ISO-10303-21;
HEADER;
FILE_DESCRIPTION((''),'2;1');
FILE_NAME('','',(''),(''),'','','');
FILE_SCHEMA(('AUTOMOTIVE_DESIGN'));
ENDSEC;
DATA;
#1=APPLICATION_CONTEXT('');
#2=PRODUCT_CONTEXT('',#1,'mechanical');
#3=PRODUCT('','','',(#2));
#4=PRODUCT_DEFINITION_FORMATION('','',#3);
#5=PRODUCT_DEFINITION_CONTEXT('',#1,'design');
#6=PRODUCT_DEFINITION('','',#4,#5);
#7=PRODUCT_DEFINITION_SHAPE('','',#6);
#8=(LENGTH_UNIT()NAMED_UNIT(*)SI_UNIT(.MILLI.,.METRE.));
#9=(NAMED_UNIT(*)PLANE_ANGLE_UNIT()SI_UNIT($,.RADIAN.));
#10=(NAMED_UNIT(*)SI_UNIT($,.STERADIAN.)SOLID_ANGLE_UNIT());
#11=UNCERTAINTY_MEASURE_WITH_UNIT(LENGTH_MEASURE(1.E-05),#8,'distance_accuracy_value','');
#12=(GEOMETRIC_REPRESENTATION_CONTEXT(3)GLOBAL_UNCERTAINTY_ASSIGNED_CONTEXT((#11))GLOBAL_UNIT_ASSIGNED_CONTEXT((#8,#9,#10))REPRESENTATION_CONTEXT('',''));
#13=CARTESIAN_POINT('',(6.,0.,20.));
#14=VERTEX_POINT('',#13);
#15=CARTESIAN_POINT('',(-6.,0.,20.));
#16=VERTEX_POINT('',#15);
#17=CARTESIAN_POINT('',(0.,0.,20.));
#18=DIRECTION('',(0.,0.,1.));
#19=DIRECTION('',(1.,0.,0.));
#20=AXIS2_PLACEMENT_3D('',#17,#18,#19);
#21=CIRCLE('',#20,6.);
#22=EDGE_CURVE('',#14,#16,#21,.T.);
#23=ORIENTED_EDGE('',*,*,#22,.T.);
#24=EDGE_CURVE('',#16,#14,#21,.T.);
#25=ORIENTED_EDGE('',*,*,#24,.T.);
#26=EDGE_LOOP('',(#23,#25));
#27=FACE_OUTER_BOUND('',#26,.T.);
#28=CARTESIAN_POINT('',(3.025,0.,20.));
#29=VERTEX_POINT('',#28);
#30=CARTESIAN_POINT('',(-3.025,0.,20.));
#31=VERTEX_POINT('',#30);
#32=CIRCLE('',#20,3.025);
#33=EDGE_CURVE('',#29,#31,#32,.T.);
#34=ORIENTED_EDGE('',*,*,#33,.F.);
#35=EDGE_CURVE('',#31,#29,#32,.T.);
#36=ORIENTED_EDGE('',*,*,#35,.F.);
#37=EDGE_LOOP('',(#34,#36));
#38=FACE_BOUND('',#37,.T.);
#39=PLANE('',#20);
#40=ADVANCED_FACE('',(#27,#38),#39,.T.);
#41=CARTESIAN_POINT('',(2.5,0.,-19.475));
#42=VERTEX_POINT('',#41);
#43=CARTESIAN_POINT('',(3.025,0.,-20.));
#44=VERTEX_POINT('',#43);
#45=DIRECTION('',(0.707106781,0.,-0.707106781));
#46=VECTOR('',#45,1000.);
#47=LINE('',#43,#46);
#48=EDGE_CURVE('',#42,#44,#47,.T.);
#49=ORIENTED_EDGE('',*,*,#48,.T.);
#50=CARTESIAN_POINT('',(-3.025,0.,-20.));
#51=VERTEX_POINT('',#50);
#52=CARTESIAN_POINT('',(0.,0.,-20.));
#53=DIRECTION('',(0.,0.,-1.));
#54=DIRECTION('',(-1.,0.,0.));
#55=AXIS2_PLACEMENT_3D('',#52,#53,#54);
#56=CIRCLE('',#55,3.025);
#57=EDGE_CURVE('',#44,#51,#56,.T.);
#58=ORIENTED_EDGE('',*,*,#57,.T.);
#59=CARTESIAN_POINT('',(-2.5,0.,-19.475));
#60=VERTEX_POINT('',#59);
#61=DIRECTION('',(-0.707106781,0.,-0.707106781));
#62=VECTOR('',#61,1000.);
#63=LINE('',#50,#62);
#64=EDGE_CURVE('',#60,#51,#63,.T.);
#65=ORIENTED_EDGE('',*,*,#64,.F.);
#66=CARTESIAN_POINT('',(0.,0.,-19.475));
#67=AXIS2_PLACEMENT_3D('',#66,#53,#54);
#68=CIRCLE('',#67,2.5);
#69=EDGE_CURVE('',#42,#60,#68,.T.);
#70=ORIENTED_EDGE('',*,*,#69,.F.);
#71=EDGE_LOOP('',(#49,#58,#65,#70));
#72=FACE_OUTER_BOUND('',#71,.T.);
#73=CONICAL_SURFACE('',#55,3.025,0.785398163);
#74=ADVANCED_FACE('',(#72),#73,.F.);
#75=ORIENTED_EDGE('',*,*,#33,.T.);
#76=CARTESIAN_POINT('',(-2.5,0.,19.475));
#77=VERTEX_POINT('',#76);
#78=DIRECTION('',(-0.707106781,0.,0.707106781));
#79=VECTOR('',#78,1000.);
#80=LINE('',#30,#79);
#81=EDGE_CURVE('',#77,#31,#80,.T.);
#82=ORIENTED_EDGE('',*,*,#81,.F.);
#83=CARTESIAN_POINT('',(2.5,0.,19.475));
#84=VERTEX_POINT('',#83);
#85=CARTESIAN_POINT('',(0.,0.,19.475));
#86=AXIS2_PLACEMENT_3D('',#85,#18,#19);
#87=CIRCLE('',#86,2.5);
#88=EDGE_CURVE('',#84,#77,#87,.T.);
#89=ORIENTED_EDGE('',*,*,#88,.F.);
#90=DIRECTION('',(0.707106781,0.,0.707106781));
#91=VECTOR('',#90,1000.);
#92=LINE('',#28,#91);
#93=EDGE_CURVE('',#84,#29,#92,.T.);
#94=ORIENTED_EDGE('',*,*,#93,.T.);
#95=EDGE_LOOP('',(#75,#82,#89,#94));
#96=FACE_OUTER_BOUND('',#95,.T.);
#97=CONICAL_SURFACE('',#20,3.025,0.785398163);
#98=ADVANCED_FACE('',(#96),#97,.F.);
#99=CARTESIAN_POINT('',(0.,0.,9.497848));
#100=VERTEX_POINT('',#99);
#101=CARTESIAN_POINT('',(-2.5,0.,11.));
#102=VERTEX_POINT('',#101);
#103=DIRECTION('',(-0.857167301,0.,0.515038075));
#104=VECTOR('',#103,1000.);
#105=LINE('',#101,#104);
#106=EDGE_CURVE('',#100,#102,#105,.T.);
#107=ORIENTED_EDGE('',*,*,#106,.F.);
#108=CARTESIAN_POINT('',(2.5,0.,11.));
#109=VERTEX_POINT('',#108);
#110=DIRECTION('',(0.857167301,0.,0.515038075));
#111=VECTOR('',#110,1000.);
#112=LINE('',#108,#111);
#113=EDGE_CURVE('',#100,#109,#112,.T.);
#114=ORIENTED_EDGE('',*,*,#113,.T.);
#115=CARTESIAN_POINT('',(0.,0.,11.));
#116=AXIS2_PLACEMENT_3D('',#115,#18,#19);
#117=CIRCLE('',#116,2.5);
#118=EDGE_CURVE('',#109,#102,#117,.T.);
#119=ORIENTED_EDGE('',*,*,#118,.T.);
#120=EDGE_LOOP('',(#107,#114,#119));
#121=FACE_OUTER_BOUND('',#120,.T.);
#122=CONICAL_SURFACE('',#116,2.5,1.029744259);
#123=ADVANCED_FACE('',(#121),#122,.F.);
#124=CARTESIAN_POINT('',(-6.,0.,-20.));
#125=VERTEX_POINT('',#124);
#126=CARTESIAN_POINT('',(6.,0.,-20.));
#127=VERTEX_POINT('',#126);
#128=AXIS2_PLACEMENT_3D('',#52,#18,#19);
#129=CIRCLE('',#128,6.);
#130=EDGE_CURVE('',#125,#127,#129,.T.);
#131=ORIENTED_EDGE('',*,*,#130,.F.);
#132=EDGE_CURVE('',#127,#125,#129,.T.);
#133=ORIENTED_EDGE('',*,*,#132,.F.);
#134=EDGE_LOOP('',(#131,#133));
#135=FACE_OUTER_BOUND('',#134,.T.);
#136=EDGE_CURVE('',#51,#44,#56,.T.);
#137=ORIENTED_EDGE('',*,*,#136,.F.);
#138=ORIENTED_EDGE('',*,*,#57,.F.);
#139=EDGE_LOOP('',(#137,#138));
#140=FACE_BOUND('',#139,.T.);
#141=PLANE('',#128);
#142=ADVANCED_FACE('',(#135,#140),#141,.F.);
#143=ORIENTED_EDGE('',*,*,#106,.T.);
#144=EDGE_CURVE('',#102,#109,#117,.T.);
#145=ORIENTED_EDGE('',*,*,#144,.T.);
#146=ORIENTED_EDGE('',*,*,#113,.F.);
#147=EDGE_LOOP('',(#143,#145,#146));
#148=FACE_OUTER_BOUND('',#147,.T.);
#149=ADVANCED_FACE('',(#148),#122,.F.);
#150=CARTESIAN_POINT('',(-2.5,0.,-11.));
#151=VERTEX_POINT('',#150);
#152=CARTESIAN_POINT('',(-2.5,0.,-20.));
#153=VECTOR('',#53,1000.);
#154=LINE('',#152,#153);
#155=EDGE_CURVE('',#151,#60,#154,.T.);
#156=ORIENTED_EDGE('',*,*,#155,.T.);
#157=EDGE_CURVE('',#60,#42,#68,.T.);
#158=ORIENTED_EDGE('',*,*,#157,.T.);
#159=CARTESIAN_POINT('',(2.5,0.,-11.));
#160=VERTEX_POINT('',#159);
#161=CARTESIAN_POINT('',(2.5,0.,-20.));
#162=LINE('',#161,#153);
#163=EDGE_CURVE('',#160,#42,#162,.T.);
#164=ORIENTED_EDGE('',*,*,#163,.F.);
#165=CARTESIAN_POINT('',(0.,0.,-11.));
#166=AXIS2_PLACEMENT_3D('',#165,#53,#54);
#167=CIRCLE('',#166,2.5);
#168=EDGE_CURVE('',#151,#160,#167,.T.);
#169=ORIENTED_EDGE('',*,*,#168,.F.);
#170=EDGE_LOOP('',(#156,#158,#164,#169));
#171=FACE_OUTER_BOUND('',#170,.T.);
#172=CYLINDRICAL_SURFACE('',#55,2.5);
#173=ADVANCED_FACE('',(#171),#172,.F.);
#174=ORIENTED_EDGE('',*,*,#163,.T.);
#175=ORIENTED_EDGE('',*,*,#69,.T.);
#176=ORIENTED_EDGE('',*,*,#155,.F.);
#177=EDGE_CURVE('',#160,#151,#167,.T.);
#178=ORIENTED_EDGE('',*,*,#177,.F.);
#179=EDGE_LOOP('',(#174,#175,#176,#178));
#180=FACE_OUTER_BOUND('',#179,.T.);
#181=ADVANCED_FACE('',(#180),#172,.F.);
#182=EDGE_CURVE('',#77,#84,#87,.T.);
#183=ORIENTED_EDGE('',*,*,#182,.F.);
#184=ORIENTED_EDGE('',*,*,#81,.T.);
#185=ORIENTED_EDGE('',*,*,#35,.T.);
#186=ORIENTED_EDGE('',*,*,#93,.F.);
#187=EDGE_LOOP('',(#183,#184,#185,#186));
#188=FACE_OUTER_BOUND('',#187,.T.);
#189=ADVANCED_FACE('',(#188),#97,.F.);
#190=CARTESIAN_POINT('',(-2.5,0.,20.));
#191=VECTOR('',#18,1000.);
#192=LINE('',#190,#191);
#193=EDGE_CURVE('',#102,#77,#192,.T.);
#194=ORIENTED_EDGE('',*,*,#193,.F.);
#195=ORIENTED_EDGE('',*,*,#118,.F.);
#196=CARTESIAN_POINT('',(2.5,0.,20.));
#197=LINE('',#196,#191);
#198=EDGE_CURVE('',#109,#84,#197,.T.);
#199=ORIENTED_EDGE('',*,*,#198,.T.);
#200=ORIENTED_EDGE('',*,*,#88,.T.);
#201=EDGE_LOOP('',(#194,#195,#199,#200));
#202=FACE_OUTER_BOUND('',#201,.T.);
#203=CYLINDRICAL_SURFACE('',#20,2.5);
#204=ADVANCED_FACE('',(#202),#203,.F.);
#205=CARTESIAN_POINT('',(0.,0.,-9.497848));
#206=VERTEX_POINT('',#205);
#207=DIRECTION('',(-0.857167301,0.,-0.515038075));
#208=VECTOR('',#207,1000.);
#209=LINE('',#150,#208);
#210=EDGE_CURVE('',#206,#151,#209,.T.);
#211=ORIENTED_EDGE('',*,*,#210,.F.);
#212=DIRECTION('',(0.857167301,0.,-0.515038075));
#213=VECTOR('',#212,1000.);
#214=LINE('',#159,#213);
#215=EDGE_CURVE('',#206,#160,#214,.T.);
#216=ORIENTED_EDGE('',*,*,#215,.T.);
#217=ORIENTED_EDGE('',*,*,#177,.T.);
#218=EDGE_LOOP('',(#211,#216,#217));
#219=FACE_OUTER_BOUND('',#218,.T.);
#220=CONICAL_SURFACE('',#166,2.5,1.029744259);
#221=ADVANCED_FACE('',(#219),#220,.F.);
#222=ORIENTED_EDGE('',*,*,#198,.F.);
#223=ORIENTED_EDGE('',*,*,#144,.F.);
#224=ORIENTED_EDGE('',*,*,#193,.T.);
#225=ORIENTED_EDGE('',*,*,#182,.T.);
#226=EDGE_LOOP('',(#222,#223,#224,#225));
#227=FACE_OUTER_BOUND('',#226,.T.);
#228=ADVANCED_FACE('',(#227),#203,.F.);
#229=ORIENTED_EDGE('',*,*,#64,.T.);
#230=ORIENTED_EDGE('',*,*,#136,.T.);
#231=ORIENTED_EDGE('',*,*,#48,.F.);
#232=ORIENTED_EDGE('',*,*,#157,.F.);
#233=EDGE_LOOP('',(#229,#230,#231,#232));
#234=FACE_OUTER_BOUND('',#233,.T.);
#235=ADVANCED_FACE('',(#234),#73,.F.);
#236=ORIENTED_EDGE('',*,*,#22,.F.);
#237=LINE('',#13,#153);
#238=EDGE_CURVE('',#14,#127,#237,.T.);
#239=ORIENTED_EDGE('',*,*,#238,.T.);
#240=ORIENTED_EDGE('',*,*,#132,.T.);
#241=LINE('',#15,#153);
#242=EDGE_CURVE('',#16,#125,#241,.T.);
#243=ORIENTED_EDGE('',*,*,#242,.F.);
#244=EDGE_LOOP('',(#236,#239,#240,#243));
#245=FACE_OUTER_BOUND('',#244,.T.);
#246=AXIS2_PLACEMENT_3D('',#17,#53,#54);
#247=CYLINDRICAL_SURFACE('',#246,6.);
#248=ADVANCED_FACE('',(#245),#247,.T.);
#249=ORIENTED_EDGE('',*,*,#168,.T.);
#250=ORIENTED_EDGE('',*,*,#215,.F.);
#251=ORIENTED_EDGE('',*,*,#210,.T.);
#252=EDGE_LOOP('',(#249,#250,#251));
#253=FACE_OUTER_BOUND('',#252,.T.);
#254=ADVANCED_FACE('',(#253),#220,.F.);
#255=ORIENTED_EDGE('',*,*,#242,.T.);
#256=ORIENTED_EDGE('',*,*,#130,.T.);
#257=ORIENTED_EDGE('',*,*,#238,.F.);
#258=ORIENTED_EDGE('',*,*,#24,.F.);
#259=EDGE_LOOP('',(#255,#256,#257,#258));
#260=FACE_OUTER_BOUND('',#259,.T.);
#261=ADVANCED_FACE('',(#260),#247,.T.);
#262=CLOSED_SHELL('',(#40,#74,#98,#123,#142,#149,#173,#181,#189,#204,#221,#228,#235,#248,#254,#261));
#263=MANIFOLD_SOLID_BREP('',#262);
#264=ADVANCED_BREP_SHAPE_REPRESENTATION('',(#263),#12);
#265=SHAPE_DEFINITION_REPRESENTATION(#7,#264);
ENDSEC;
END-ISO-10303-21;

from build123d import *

# Parameters (mm, degrees)
SKETCH_1_R      = 6
EXTRUDE_1_DEPTH = 20


with BuildPart() as part:
    # 草图1 → 凸台-拉伸1 (new, symmetric)
    with BuildSketch(Plane.XY):
        Circle(SKETCH_1_R)
    extrude(amount=EXTRUDE_1_DEPTH, both=True)

    # 草图3 → M6 螺纹孔1 (revolve, cut)
    with BuildSketch(Plane(origin=(0, 0, 20), x_dir=(0, -1, 0), z_dir=(1, 0, 0))):
        Polygon((0, 0), (0, 10.502151548), (2.5, 9), (2.5, 0.525), (3.025, 0), align=None)
    hole_wizard_m6_1 = revolve(axis=Axis((0, 0, 26.35), (0, 0, -1)), mode=Mode.SUBTRACT)

    # 镜向1: M6 螺纹孔1 across plane
    add(hole_wizard_m6_1.mirror(Plane.XY), mode=Mode.SUBTRACT)


solid = part.part
